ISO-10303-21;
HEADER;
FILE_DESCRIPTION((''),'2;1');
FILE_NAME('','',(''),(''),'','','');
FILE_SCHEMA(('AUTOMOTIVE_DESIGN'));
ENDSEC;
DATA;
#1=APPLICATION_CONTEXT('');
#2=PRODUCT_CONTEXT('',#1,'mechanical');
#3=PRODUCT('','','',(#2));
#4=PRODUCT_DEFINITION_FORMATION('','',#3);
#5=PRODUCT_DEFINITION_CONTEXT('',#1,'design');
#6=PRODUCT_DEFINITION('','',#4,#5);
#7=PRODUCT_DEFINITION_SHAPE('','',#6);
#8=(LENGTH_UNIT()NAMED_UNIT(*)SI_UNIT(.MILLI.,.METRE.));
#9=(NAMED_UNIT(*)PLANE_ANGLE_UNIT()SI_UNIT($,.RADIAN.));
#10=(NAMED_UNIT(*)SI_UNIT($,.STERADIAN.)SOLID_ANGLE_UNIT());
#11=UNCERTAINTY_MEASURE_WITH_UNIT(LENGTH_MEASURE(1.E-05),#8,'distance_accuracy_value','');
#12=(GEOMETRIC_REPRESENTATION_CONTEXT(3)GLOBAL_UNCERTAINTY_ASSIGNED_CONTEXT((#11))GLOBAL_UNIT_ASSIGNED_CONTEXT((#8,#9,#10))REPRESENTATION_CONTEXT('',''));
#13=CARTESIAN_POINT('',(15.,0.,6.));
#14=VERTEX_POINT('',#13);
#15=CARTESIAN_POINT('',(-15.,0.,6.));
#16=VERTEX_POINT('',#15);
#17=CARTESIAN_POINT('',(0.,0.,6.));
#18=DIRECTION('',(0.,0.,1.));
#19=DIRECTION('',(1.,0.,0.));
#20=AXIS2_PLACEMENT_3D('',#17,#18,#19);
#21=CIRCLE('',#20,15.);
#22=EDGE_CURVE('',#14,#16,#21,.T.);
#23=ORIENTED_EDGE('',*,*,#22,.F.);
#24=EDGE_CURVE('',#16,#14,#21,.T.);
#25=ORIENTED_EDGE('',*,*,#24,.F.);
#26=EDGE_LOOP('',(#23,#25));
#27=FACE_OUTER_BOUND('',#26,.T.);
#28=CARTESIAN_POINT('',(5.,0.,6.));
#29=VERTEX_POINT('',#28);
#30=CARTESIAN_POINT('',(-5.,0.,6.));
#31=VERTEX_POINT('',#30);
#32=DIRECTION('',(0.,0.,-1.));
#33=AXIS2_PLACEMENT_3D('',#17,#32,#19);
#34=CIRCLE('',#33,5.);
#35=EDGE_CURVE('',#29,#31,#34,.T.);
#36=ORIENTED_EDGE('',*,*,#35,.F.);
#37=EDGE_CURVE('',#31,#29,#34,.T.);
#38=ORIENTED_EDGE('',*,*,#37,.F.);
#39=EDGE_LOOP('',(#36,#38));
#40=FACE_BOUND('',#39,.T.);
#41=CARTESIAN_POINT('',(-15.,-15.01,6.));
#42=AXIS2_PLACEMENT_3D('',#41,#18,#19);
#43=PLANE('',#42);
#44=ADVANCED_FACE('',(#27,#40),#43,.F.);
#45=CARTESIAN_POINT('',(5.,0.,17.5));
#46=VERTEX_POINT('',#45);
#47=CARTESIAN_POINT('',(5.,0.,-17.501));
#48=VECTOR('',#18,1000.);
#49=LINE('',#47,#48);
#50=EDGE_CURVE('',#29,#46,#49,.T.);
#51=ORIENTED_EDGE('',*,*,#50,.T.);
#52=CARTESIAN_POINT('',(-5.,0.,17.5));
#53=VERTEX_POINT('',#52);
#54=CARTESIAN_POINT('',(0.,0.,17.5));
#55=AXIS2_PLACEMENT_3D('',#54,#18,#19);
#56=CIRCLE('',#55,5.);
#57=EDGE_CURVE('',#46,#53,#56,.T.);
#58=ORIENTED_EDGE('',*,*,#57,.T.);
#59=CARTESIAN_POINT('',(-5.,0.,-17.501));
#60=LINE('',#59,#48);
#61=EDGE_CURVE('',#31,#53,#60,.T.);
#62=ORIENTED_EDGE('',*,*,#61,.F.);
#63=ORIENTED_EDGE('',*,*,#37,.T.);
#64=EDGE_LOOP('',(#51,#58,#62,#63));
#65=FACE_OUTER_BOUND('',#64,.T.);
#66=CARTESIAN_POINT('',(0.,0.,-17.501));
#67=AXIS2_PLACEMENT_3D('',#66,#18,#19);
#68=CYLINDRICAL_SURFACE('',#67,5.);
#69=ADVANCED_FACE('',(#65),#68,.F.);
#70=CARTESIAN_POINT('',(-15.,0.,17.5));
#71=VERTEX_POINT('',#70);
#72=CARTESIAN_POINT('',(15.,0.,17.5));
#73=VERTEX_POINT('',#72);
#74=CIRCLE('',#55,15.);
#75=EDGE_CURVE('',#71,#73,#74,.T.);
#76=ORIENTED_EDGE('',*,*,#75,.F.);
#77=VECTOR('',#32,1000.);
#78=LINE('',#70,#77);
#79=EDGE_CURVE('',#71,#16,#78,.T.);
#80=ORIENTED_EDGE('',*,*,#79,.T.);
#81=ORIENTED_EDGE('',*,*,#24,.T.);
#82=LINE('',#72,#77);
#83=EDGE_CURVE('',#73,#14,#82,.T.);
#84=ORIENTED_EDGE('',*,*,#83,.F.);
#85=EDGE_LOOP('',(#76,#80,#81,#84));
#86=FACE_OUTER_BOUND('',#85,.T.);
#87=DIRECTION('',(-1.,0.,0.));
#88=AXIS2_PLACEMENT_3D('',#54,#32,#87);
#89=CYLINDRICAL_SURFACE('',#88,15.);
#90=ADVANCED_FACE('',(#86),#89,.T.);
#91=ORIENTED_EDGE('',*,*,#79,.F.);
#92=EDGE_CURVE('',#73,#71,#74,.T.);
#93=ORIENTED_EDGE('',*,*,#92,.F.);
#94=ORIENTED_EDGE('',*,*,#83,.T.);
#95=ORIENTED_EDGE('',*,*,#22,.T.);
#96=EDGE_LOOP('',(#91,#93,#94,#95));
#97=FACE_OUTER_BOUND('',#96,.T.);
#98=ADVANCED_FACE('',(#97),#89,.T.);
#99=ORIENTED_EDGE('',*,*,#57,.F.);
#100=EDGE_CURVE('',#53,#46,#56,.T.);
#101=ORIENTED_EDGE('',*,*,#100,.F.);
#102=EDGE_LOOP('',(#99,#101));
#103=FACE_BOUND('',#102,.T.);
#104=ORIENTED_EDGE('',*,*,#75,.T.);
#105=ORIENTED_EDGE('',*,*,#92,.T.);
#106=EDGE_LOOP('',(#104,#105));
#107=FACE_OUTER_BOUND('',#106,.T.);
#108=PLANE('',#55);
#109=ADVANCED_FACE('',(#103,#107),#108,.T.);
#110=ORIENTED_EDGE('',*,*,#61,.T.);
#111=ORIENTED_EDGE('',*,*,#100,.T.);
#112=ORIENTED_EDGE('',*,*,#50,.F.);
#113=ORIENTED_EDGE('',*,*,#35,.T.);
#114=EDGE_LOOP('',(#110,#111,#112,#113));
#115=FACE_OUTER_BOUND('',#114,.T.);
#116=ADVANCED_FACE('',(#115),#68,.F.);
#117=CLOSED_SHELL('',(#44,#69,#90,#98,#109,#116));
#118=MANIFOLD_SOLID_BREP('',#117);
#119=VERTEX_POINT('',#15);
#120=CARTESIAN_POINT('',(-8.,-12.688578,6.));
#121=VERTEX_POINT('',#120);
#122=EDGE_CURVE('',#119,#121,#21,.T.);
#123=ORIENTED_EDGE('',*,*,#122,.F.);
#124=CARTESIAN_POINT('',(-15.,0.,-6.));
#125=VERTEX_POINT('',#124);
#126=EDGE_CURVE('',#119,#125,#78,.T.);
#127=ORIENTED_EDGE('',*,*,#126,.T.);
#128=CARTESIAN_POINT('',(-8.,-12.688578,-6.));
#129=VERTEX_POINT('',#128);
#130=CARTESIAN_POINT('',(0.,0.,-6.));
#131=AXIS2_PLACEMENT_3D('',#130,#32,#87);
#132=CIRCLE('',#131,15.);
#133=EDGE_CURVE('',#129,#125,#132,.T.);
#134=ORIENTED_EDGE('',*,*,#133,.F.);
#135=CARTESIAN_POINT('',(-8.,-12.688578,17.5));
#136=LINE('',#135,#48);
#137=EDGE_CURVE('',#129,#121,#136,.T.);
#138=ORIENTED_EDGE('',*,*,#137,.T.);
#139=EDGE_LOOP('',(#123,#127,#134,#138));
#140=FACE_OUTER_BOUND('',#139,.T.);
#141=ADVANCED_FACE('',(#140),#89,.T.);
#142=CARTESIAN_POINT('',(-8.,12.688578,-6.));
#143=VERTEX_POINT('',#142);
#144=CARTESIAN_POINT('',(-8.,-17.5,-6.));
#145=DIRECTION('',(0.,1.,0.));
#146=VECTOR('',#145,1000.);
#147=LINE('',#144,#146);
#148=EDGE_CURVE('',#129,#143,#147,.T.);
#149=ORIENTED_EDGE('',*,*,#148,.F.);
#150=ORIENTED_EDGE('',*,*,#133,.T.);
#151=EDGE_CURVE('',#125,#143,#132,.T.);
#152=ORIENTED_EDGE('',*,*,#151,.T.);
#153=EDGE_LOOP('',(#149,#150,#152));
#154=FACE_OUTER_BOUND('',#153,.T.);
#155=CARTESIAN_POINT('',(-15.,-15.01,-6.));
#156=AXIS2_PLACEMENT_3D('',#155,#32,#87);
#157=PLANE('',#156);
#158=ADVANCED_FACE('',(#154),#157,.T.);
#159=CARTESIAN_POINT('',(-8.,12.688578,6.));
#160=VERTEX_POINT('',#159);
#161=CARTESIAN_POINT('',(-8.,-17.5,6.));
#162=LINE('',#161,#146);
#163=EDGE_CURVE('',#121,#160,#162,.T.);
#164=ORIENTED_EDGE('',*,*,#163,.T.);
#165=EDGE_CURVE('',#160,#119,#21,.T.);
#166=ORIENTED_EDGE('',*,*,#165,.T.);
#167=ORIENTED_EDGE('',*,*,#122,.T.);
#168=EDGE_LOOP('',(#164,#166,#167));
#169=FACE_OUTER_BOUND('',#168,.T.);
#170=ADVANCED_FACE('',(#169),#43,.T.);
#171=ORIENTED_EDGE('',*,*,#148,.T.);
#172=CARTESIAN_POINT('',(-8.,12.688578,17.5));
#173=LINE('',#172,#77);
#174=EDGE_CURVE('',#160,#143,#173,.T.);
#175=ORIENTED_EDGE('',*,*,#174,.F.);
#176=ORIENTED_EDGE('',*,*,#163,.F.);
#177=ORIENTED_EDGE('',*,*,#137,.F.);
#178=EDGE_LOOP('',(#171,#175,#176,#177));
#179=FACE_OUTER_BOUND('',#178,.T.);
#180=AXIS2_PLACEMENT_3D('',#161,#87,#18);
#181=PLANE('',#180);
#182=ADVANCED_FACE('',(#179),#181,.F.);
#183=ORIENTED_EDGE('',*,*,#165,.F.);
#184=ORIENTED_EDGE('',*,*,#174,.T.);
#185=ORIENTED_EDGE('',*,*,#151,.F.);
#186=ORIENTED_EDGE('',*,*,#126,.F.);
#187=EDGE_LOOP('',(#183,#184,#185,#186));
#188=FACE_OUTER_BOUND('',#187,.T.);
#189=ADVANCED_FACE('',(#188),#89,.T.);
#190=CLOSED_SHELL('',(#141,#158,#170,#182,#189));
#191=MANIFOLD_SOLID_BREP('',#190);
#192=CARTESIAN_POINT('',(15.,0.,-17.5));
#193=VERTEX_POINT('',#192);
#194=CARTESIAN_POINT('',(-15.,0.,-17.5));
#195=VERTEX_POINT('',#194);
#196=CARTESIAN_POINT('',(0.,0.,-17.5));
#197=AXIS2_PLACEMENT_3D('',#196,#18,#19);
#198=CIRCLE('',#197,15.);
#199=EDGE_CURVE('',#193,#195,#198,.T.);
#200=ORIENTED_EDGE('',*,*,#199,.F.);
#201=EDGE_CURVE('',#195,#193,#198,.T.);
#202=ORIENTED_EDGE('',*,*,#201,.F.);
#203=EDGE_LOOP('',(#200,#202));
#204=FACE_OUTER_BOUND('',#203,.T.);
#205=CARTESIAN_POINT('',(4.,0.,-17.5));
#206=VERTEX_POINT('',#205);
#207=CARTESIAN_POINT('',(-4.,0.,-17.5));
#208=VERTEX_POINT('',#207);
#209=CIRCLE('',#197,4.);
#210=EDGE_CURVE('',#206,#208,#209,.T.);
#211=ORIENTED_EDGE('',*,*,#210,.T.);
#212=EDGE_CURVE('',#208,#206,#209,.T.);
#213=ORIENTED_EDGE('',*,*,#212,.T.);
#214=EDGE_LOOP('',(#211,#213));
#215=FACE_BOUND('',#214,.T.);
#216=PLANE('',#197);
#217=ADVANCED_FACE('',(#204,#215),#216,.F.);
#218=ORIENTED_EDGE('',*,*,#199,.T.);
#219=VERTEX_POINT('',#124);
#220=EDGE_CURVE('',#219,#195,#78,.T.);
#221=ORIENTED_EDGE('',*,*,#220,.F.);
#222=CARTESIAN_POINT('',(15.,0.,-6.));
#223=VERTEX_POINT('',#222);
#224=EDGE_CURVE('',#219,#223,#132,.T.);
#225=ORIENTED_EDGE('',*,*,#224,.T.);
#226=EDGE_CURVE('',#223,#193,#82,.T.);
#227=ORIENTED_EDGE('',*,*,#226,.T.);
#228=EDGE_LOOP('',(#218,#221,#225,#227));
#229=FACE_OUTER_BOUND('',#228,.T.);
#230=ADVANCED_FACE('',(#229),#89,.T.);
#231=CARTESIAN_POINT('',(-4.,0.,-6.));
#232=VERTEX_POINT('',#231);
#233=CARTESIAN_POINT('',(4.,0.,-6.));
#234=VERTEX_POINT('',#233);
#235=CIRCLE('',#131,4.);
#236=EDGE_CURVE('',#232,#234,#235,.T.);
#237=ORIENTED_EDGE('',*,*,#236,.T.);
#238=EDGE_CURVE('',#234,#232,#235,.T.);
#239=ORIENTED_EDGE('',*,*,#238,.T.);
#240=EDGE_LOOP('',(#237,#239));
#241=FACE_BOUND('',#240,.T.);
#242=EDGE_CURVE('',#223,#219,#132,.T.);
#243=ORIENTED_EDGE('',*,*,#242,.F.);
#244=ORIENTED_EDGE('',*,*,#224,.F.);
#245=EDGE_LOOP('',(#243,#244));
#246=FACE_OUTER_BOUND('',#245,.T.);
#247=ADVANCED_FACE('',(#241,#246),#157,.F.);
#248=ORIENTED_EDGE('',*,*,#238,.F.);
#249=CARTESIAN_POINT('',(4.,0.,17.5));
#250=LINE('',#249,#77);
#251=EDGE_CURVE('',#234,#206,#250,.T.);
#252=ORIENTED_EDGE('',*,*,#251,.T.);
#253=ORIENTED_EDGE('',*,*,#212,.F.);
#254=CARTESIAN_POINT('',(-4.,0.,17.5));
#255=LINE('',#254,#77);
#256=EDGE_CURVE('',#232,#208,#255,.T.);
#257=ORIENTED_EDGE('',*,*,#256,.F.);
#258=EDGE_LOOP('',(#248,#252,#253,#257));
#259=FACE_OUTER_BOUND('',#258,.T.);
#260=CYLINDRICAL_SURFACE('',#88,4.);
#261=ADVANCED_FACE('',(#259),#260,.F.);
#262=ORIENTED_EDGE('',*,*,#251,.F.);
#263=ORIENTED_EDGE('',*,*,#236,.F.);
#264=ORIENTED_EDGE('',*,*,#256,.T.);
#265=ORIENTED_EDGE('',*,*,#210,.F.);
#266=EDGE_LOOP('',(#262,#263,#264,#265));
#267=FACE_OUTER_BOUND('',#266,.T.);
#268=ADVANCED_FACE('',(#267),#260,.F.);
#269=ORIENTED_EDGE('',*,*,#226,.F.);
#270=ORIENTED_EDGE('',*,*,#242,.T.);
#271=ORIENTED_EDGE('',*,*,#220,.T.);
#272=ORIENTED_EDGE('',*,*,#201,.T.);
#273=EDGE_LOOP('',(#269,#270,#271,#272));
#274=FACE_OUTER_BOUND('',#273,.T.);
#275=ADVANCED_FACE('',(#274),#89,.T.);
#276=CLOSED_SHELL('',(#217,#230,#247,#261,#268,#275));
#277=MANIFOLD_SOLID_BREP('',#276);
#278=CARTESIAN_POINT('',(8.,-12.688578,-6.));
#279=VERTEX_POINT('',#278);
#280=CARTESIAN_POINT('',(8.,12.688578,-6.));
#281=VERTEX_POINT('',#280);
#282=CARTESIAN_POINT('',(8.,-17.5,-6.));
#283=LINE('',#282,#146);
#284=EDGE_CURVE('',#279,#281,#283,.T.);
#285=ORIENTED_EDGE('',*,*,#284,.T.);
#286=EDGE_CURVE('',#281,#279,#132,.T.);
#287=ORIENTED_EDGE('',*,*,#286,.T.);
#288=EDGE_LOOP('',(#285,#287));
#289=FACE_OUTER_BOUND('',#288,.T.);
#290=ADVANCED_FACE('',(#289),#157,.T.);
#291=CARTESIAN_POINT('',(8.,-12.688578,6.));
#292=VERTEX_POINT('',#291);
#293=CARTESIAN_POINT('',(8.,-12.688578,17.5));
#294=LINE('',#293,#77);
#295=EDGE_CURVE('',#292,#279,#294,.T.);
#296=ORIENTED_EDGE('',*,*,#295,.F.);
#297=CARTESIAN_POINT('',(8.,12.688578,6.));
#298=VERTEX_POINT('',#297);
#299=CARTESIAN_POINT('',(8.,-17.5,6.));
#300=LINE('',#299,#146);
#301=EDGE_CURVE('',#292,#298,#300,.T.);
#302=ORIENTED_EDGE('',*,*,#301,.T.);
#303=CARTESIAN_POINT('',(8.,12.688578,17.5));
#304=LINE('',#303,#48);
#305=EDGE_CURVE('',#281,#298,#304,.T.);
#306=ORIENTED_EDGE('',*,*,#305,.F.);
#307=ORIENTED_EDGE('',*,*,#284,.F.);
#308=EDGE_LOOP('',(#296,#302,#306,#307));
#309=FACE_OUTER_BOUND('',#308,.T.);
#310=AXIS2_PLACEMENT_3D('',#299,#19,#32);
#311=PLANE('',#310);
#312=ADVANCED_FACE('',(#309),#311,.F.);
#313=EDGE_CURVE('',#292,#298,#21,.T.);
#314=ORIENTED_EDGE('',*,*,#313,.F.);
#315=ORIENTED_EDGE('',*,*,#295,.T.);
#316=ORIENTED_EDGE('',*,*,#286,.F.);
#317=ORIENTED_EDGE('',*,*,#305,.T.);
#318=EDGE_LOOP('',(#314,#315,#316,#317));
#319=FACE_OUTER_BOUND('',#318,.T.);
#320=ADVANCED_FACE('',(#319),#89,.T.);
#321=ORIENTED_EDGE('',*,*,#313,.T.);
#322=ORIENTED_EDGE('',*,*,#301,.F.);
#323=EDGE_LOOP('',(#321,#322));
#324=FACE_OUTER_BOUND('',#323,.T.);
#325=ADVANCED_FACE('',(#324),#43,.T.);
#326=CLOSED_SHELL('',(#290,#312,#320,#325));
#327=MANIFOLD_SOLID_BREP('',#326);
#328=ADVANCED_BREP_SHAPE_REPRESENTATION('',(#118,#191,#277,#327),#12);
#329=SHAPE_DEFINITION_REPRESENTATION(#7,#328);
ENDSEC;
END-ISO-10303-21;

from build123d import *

# Parameters (mm, degrees)
SKETCH1_R              = 15
SKETCH1_R_2            = 4
BOSS_EXTRUDE1_DEPTH    = 17.5
SKETCH2_W              = 16
SKETCH2_H              = 12
CUT_EXTRUDE1_DEPTH     = 17.5
CUT_EXTRUDE2_REACH     = 42.927
SKETCH3_R              = 5
SPLIT1_SURFACE_1_BACK  = 56
SPLIT1_SURFACE_1_DEPTH = 112
SPLIT1_SURFACE_2_BACK  = 56
SPLIT1_SURFACE_2_DEPTH = 112


with BuildPart() as part:
    # Sketch1 → Boss-Extrude1 (new, symmetric)
    with BuildSketch(Plane.XY):
        Circle(SKETCH1_R)
        Circle(SKETCH1_R_2, mode=Mode.SUBTRACT)
    extrude(amount=BOSS_EXTRUDE1_DEPTH, both=True)

    # Sketch2 → Cut-Extrude1 (cut, symmetric)
    with BuildSketch(Plane(origin=(0, 0, 0), x_dir=(1, 0, 0), z_dir=(0, 1, 0))):
        Rectangle(SKETCH2_W, SKETCH2_H)
    extrude(amount=CUT_EXTRUDE1_DEPTH, both=True, mode=Mode.SUBTRACT)

    # Sketch3 → Cut-Extrude2 (cut, up to next)
    with BuildSketch(Plane.XY.offset(17.5), mode=Mode.PRIVATE) as cut_extrude2_sk1:
        Circle(SKETCH3_R)
    cut_extrude2_tool1 = extrude(cut_extrude2_sk1.sketch, amount=-CUT_EXTRUDE2_REACH, mode=Mode.PRIVATE) & part.part
    add(cut_extrude2_tool1.solids().sort_by_distance((0, 0, 17.5))[0], mode=Mode.SUBTRACT)


with BuildPart() as body_2:
    # Split1: the piece behind the surface
    add(part.part)
    # Split1 surface: a surface, the sketch's curves swept straight by 112 mm
    with BuildLine(Plane(origin=(0, 0, 0), x_dir=(1, 0, 0), z_dir=(0, 1, 0)).offset(-SPLIT1_SURFACE_1_BACK), mode=Mode.PRIVATE) as split1_surface_1_path:
        Line((-15, 6), (15, 6))
        Line((15, 6), (15, -6))
        Line((15, -6), (-15, -6))
        Line((-15, -6), (-15, 6))
    split1_surface_1 = Shell.extrude(split1_surface_1_path.wire(), (0 * SPLIT1_SURFACE_1_DEPTH, 1 * SPLIT1_SURFACE_1_DEPTH, 0 * SPLIT1_SURFACE_1_DEPTH))
    split(bisect_by=split1_surface_1, keep=Keep.BOTTOM)


with BuildPart() as part_1:
    add(part.part)

    # Split1: split by a surface, the side it looks to stays
    # Split1 surface: a surface, the sketch's curves swept straight by 112 mm
    with BuildLine(Plane(origin=(0, 0, 0), x_dir=(1, 0, 0), z_dir=(0, 1, 0)).offset(-SPLIT1_SURFACE_2_BACK), mode=Mode.PRIVATE) as split1_surface_2_path:
        Line((-15, 6), (15, 6))
        Line((15, 6), (15, -6))
        Line((15, -6), (-15, -6))
        Line((-15, -6), (-15, 6))
    split1_surface_2 = Shell.extrude(split1_surface_2_path.wire(), (0 * SPLIT1_SURFACE_2_DEPTH, 1 * SPLIT1_SURFACE_2_DEPTH, 0 * SPLIT1_SURFACE_2_DEPTH))
    split(bisect_by=split1_surface_2, keep=Keep.TOP)


solid = Compound([body_2.part, part_1.part])
